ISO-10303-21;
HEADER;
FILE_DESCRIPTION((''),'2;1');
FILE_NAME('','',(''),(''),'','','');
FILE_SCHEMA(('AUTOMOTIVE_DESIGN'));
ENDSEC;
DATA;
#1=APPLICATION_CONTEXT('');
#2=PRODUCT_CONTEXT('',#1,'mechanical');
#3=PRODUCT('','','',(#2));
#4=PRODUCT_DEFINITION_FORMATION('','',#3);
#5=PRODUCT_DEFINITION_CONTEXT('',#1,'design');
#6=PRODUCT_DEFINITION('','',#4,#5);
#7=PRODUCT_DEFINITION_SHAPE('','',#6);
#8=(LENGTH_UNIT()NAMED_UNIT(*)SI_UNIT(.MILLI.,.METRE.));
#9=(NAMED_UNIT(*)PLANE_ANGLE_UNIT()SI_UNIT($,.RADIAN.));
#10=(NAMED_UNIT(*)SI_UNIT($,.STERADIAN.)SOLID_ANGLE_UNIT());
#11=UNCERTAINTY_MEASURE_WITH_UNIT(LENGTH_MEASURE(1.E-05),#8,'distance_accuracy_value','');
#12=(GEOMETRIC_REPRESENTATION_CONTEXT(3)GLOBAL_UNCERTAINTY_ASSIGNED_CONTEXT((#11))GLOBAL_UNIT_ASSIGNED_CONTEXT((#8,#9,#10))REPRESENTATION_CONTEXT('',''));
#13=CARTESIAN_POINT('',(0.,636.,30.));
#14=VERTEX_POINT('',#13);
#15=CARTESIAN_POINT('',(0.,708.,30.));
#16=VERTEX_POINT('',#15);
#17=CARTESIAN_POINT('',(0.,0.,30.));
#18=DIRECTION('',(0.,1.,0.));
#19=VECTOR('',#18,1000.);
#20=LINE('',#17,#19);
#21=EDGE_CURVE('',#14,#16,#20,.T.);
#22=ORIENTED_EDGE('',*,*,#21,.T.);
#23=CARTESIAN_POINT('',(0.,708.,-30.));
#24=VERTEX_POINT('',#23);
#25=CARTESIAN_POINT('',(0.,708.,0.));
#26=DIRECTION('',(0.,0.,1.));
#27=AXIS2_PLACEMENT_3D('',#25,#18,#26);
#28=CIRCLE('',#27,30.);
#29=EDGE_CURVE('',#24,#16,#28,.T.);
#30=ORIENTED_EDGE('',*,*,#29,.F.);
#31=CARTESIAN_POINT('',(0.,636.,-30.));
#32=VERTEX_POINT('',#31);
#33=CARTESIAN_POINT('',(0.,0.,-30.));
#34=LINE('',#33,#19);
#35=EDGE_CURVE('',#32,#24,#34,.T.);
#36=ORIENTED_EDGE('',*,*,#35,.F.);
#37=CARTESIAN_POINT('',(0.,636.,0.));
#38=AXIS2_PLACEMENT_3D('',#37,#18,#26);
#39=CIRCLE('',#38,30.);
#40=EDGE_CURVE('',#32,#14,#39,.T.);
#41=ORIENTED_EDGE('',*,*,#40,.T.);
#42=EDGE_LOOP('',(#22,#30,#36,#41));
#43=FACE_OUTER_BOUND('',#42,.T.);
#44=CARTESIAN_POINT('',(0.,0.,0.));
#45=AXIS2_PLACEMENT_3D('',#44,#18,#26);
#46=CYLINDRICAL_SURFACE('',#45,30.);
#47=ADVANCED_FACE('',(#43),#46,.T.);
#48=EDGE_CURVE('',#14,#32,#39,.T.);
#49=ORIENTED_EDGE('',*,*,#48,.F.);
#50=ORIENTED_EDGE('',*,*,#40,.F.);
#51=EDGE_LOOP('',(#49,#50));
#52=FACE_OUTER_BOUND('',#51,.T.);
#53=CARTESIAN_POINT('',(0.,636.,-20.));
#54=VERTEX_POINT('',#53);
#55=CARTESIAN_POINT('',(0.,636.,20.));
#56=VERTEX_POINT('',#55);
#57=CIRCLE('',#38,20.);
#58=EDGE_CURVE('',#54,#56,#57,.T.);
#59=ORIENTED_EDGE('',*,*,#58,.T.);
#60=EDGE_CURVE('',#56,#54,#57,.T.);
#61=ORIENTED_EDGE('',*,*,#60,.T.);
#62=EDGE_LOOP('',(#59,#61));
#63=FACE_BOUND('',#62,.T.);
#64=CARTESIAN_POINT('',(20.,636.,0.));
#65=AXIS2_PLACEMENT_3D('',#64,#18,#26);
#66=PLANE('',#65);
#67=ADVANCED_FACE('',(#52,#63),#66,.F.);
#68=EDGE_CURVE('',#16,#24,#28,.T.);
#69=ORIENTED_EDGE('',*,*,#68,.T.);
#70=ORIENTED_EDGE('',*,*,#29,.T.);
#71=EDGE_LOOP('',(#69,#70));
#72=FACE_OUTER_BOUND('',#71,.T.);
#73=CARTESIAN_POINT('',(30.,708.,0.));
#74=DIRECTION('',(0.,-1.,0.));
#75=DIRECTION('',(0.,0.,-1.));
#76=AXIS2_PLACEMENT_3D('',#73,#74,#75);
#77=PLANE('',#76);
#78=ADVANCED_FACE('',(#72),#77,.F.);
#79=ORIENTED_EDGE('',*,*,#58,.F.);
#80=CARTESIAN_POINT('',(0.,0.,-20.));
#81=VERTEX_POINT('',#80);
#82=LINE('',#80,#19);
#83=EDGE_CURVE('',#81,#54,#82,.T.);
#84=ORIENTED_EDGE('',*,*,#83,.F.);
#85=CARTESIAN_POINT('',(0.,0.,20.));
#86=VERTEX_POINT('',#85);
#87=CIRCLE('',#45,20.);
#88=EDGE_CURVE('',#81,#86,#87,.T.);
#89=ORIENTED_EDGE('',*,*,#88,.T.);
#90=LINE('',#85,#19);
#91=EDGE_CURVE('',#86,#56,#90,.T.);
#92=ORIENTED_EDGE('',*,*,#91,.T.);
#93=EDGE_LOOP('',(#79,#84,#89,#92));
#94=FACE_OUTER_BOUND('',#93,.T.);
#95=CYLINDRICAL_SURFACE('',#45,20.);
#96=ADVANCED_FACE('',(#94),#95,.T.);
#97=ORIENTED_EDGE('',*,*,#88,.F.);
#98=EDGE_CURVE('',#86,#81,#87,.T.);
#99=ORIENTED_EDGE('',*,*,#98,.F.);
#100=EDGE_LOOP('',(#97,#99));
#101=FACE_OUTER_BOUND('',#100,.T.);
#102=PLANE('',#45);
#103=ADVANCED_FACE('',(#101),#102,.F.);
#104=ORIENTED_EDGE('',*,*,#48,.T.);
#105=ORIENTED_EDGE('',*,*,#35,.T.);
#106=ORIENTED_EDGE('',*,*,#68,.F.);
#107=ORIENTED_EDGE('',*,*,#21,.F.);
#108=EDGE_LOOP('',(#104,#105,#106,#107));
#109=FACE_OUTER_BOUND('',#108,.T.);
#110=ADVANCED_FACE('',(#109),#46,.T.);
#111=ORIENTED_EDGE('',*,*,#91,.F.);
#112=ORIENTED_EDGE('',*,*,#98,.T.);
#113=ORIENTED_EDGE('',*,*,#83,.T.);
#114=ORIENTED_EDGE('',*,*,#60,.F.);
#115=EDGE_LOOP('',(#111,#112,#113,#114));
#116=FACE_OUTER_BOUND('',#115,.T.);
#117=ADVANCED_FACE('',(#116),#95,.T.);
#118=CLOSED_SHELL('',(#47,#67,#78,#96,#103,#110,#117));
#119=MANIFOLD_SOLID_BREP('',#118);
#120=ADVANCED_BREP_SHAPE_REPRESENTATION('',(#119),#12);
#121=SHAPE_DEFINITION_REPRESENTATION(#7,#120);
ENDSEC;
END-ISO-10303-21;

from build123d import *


with BuildPart() as part:
    # Sketch1 → Revolve1 (revolve)
    with BuildSketch(Plane.XY, mode=Mode.PRIVATE) as revolve1_sk:
        Polygon((0, 0), (20, 0), (20, 636), (30, 636), (30, 708), (0, 708), align=None)
    revolve(revolve1_sk.sketch.rotate(Axis((0, 0, 0), (0, -1, 0)), 90), axis=Axis((0, 0, 0), (0, -1, 0)))


solid = part.part
